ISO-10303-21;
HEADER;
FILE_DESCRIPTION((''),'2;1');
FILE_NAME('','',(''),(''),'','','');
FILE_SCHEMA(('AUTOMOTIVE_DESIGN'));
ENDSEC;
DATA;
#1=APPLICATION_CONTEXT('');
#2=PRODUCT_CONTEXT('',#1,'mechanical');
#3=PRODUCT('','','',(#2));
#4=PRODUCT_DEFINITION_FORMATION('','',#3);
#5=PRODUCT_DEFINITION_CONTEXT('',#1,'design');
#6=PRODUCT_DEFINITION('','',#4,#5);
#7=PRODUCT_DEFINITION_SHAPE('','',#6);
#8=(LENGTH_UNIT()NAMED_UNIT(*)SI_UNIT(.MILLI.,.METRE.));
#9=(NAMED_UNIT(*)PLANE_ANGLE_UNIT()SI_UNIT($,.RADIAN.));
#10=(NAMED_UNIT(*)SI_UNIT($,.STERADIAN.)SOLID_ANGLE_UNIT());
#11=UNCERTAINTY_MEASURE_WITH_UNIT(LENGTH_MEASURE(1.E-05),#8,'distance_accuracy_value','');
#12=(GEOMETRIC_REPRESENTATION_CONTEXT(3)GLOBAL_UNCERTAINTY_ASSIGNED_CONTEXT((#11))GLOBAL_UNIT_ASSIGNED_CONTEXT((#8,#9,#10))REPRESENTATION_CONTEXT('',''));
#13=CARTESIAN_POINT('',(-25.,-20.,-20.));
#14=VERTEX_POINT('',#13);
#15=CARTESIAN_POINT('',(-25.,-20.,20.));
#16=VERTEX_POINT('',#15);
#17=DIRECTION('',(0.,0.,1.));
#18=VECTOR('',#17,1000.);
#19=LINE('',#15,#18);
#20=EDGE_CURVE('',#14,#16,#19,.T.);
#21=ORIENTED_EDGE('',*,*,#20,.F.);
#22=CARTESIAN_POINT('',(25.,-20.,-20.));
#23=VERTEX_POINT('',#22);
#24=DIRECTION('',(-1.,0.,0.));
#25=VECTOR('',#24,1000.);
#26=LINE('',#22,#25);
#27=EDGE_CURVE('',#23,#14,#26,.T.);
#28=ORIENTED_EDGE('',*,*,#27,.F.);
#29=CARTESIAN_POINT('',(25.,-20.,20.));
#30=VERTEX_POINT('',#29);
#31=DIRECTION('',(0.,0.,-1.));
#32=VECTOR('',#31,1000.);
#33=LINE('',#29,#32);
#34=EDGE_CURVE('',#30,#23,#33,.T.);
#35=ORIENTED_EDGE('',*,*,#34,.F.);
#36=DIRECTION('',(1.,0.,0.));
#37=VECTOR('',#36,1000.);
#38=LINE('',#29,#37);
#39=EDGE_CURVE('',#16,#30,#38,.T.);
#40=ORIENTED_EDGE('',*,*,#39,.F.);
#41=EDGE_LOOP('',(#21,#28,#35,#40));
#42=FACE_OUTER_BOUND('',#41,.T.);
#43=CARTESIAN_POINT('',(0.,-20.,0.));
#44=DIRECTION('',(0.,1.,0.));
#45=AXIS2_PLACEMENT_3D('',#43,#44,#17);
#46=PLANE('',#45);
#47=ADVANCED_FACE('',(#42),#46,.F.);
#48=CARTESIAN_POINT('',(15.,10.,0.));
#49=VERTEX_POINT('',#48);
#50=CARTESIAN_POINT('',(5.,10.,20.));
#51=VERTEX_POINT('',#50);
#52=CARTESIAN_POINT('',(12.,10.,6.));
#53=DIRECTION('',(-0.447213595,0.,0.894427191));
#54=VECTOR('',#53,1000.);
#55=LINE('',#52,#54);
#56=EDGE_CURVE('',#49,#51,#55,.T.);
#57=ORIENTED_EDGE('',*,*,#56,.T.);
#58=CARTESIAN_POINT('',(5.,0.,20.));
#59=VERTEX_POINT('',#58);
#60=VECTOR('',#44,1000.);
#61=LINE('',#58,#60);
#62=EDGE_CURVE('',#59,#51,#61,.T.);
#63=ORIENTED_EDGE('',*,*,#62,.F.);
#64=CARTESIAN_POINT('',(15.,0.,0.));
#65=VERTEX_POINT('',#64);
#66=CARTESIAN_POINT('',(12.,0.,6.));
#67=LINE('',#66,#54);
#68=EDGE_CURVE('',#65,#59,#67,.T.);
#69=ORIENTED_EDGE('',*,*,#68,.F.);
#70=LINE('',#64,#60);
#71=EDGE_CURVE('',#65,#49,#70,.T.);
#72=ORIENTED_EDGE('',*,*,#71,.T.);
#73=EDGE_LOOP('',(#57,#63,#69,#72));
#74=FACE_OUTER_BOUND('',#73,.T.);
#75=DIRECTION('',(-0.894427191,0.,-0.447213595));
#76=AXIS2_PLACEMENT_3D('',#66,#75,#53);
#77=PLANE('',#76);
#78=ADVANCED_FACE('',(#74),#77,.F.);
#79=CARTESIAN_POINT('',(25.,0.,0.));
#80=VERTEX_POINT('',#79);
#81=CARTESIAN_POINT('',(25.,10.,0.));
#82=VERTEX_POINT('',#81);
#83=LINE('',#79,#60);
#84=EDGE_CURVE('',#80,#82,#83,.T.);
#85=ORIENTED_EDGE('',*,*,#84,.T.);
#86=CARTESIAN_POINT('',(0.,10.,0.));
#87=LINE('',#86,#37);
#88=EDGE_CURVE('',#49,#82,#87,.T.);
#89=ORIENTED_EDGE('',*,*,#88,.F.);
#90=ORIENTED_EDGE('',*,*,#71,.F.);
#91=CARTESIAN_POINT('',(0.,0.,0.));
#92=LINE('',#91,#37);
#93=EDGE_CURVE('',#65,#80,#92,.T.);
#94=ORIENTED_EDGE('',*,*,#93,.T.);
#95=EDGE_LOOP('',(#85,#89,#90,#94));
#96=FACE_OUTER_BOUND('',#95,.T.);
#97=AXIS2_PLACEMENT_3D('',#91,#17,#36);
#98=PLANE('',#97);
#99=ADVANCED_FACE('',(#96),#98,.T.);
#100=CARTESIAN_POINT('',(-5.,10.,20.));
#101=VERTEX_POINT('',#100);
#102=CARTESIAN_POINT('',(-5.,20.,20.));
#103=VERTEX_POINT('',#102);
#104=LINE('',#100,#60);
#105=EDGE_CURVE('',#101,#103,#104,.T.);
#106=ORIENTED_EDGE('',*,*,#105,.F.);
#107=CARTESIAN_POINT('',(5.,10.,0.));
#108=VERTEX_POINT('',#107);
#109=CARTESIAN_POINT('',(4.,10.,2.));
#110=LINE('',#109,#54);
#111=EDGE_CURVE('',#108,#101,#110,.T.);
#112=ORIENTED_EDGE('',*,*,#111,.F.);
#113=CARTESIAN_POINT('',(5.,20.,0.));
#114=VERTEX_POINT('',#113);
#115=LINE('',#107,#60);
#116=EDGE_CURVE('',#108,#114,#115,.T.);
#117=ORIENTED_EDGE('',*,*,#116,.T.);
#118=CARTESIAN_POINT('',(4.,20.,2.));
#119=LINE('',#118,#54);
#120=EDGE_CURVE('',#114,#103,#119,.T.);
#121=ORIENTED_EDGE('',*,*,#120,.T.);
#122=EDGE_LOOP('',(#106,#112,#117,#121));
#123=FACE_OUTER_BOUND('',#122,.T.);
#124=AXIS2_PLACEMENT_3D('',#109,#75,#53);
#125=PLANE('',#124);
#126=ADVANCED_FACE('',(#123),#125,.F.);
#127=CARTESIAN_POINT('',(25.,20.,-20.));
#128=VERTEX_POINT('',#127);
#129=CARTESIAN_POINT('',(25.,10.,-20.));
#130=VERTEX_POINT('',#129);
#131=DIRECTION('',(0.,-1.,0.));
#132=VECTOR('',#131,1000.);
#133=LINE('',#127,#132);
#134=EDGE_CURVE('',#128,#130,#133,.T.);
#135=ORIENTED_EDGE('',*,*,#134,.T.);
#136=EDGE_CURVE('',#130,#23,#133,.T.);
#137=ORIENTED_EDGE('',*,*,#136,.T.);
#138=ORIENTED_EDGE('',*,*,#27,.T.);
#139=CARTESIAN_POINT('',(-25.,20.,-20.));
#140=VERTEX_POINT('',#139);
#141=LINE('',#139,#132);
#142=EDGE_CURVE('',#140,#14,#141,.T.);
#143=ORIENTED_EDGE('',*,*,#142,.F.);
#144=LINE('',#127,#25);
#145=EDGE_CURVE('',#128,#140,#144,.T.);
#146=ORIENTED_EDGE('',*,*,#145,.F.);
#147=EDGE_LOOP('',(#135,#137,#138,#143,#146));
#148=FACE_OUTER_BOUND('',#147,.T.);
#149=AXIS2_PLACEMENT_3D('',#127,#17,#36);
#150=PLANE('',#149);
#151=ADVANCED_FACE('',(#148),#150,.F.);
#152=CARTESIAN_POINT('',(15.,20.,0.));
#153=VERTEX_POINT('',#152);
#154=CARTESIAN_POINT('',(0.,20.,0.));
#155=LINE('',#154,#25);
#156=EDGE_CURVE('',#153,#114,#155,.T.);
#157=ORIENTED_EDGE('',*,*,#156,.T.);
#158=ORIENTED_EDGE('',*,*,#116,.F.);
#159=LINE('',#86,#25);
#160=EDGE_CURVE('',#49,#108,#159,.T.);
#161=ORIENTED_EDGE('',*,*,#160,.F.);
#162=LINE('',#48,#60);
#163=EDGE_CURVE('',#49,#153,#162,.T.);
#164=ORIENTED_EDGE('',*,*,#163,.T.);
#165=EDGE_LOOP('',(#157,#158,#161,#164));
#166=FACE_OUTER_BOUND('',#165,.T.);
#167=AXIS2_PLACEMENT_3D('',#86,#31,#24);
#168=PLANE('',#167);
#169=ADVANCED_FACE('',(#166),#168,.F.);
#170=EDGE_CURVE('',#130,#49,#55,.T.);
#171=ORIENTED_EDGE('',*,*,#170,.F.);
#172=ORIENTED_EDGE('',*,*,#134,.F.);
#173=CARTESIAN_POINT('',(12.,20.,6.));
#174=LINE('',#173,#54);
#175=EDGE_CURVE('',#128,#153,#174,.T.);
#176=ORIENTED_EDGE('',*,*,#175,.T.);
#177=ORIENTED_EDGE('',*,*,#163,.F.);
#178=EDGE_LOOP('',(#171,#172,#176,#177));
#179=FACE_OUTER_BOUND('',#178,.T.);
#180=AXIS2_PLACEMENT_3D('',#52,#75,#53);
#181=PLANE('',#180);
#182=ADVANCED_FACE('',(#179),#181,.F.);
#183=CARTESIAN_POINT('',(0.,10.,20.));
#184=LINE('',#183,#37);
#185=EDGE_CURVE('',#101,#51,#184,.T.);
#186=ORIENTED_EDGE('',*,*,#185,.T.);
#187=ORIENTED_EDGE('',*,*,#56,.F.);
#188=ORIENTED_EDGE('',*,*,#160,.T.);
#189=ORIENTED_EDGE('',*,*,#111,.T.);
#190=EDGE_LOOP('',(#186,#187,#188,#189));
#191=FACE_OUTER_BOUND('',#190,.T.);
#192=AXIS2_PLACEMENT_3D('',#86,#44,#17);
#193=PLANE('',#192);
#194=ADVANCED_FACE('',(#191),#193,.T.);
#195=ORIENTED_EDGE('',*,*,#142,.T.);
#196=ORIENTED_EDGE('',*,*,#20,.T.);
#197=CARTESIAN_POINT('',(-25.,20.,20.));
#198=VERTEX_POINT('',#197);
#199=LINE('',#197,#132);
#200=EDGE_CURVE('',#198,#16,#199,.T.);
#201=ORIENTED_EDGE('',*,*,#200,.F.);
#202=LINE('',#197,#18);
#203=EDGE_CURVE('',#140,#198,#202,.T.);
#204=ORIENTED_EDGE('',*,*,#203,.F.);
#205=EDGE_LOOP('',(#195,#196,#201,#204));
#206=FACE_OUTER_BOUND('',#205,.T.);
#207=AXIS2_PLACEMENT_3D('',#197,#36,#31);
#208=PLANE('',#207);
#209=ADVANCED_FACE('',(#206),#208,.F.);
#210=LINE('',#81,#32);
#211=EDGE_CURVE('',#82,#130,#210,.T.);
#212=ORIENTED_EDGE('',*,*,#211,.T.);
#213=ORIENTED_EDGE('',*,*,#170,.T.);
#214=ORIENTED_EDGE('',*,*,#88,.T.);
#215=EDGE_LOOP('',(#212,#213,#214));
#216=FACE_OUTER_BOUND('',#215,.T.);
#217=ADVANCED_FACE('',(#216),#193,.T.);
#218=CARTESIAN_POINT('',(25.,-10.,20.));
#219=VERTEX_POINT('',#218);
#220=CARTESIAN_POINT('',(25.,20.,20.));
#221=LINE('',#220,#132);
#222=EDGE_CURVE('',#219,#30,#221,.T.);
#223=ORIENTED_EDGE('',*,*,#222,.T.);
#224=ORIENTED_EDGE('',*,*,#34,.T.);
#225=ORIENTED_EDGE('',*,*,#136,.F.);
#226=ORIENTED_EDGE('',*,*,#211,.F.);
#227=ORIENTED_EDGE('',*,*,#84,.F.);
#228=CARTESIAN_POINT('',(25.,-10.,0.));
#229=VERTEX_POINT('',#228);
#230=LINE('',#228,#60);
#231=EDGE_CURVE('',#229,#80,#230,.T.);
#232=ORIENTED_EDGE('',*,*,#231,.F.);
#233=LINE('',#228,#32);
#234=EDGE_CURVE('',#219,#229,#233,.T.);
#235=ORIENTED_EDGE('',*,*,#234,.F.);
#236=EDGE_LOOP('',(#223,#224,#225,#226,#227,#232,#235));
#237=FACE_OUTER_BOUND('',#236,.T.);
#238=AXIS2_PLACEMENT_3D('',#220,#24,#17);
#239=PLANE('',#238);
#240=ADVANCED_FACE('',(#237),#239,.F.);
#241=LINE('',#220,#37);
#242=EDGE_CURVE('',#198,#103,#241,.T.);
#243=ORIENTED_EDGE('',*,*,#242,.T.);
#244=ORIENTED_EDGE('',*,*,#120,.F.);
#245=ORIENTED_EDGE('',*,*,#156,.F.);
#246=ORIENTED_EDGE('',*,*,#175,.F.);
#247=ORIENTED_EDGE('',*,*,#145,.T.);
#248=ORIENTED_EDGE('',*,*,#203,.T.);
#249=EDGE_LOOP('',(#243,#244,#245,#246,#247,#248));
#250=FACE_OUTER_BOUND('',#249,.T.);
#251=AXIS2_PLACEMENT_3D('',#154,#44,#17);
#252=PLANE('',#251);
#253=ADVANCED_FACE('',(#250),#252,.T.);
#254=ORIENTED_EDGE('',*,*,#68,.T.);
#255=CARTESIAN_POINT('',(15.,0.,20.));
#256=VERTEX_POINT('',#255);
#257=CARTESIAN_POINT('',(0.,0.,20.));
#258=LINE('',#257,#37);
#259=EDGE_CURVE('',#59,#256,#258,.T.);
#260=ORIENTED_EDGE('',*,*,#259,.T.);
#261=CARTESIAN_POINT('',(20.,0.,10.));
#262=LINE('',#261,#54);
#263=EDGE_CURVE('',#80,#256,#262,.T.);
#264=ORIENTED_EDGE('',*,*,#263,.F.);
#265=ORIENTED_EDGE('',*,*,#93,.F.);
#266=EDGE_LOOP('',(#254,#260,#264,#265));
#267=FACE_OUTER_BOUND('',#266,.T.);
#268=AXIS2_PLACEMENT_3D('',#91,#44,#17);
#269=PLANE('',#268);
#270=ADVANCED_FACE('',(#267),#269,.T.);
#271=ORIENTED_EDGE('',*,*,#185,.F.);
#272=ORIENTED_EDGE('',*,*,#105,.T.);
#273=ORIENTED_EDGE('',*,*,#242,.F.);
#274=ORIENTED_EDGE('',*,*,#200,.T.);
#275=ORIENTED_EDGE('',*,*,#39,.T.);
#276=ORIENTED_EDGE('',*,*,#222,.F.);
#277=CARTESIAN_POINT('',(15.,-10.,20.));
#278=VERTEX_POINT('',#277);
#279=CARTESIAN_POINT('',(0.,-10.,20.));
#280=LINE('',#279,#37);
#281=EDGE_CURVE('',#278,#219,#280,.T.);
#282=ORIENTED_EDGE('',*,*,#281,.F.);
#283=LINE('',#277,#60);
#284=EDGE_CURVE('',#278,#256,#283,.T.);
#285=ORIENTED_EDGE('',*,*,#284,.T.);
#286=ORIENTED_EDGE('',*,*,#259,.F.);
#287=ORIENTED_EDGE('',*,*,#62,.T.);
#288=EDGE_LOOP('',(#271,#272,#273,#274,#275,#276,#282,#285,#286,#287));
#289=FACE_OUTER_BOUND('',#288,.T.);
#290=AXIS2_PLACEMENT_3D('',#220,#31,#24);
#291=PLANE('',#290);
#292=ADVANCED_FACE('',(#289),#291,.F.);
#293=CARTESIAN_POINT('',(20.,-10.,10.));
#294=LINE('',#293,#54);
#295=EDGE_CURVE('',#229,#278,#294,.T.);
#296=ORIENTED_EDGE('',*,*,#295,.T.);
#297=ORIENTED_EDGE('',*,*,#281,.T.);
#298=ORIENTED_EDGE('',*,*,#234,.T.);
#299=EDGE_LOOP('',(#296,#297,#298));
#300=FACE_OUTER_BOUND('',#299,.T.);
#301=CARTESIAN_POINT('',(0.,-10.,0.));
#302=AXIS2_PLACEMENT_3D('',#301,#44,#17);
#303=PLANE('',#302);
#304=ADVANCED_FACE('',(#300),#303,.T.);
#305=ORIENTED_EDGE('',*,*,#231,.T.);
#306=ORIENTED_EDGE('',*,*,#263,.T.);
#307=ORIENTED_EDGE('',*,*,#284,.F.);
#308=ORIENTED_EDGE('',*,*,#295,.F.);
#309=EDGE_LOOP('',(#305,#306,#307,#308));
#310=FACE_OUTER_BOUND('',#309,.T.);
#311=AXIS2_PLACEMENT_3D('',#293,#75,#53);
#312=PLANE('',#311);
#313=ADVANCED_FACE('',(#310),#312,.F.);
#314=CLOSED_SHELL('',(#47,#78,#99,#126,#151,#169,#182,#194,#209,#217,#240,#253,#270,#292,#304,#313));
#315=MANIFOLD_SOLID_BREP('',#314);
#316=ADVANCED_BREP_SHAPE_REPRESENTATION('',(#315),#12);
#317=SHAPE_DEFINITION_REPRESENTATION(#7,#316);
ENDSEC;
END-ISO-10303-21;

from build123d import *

# Parameters (mm, degrees)
BASE_BLOCK_PROFILE_W      = 50
BASE_BLOCK_PROFILE_H      = 40
BASE_BLOCK_50X40X40_DEPTH = 20
STEP_CUT_1_DEPTH          = 10
STEP_CUT_2_DEPTH          = 10
STEP_CUT_3_DEPTH          = 10


with BuildPart() as part:
    # Base Block Profile → Base Block 50x40x40 (new, symmetric)
    with BuildSketch(Plane(origin=(0, 0, 0), x_dir=(1, 0, 0), z_dir=(0, 1, 0))):
        Rectangle(BASE_BLOCK_PROFILE_W, BASE_BLOCK_PROFILE_H)
    extrude(amount=BASE_BLOCK_50X40X40_DEPTH, both=True)

    # Step Cut 1 Profile → Step Cut 1 (cut)
    with BuildSketch(Plane(origin=(0, 20, 0), x_dir=(1, 0, 0), z_dir=(0, 1, 0))):
        Polygon((25, 20), (15, 0), (5, 0), (-5, -20), (25, -20), align=None)
    extrude(amount=-STEP_CUT_1_DEPTH, mode=Mode.SUBTRACT)

    # Step Cut 2 Profile → Step Cut 2 (cut)
    with BuildSketch(Plane(origin=(0, 10, 0), x_dir=(1, 0, 0), z_dir=(0, 1, 0))):
        Polygon((25, 0), (15, 0), (5, -20), (25, -20), align=None)
    extrude(amount=-STEP_CUT_2_DEPTH, mode=Mode.SUBTRACT)

    # Step Cut 3 Profile → Step Cut 3 (cut)
    with BuildSketch(Plane(origin=(0, 0, 0), x_dir=(1, 0, 0), z_dir=(0, 1, 0))):
        Polygon((25, -20), (25, 0), (15, -20), align=None)
    extrude(amount=-STEP_CUT_3_DEPTH, mode=Mode.SUBTRACT)


solid = part.part
